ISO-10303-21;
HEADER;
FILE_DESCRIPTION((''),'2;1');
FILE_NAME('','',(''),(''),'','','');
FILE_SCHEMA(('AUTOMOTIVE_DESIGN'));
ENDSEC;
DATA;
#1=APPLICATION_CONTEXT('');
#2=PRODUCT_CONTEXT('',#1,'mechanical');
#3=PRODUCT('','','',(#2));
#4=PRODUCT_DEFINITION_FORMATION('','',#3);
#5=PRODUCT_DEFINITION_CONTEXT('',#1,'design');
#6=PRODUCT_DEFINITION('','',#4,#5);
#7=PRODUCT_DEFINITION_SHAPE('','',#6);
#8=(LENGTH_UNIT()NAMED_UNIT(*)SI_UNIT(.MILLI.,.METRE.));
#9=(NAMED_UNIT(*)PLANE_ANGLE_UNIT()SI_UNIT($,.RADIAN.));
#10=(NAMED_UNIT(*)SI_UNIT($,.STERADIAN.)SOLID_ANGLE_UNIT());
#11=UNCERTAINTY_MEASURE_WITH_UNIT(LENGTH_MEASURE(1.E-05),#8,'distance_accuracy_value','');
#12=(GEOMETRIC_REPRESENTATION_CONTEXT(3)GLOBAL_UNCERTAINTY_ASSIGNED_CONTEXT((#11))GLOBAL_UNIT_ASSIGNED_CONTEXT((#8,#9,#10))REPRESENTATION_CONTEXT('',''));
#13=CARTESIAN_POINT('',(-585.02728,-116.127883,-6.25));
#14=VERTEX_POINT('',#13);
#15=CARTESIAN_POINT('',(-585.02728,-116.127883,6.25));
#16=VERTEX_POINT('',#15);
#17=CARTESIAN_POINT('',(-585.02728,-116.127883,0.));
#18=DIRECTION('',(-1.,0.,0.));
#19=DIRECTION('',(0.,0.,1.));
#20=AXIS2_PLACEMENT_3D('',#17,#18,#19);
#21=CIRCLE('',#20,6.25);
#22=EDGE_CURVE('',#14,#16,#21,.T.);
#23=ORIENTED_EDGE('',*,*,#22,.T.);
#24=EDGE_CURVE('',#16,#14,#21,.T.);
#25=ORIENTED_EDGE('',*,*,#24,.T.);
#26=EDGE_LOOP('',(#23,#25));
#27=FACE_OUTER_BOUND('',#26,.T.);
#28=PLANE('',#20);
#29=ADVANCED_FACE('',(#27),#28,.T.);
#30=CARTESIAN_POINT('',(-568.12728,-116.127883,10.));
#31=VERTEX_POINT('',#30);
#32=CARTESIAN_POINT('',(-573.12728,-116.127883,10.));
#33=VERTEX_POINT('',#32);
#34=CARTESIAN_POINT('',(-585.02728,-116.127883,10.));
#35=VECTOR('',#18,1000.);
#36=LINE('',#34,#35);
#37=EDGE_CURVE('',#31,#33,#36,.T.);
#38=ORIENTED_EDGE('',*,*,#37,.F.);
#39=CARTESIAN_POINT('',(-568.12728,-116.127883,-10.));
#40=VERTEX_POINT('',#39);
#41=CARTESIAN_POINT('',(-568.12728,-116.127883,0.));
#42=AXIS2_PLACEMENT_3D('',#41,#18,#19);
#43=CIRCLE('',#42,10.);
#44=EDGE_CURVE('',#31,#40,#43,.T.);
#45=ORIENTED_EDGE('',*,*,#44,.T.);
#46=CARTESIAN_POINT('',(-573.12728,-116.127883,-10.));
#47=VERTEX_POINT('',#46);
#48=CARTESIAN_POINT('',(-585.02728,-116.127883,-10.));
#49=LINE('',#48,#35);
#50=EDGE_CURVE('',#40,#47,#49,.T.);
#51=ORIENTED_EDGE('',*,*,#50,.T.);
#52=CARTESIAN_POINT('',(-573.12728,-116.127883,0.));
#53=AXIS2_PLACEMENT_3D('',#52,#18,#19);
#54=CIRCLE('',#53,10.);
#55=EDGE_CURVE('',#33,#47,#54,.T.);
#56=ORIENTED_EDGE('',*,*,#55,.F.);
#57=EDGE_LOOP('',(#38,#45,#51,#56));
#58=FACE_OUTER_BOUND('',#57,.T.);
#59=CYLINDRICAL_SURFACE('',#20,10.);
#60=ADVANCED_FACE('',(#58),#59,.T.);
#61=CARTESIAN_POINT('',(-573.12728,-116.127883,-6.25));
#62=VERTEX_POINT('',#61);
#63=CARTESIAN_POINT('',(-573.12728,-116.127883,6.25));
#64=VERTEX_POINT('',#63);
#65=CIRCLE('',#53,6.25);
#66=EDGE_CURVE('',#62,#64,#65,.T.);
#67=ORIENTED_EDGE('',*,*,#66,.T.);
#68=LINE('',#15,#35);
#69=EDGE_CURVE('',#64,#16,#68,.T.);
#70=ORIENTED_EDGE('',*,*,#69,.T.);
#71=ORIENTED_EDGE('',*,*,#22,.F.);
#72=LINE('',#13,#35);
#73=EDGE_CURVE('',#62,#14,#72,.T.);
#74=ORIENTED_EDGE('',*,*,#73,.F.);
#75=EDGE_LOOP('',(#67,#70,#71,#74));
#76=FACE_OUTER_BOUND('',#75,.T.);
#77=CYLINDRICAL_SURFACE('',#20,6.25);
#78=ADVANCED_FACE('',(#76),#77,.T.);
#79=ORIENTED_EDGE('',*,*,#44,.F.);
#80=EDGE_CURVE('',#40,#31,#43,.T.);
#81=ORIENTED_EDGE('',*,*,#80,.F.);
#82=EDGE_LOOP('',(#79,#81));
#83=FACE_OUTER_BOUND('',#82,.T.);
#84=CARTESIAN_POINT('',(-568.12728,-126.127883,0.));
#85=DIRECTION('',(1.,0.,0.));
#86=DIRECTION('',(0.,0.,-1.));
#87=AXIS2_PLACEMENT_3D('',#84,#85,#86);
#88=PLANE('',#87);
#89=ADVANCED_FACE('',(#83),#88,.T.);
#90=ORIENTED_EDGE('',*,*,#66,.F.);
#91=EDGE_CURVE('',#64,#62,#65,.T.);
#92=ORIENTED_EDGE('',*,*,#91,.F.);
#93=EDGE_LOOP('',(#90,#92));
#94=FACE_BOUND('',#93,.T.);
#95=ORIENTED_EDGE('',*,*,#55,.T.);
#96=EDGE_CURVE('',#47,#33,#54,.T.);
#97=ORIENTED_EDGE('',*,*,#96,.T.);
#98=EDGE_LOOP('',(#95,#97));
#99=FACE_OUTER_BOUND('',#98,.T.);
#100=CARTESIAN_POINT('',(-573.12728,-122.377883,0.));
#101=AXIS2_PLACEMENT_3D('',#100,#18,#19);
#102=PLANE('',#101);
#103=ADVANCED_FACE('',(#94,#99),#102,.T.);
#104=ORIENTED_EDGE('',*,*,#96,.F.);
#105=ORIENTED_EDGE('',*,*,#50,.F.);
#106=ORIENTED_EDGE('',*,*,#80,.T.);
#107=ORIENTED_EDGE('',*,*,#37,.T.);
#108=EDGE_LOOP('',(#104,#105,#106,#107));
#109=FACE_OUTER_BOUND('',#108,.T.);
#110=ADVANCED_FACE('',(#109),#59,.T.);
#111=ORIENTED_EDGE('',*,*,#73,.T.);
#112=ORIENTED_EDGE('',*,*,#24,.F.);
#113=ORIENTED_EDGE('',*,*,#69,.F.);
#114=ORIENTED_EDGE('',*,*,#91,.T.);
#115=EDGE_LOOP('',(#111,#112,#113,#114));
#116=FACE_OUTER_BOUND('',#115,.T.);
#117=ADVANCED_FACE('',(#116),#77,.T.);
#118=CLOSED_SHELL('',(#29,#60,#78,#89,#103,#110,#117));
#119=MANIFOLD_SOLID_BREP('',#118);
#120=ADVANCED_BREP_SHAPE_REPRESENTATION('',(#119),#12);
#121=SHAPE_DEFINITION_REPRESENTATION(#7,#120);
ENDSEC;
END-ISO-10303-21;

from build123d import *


with BuildPart() as part:
    # Sketch1 → Revolve1 (revolve)
    with BuildSketch(Plane.XY, mode=Mode.PRIVATE) as revolve1_sk:
        Polygon((-585.02727965, -122.37788349), (-573.12727965, -122.37788349), (-573.12727965, -126.12788349), (-568.12727965, -126.12788349), (-568.12727965, -116.12788349), (-585.02727965, -116.12788349), align=None)
    revolve(revolve1_sk.sketch.rotate(Axis((-585.02727965, -116.12788349, 0), (1, 0, 0)), 270), axis=Axis((-585.02727965, -116.12788349, 0), (1, 0, 0)))


solid = part.part
